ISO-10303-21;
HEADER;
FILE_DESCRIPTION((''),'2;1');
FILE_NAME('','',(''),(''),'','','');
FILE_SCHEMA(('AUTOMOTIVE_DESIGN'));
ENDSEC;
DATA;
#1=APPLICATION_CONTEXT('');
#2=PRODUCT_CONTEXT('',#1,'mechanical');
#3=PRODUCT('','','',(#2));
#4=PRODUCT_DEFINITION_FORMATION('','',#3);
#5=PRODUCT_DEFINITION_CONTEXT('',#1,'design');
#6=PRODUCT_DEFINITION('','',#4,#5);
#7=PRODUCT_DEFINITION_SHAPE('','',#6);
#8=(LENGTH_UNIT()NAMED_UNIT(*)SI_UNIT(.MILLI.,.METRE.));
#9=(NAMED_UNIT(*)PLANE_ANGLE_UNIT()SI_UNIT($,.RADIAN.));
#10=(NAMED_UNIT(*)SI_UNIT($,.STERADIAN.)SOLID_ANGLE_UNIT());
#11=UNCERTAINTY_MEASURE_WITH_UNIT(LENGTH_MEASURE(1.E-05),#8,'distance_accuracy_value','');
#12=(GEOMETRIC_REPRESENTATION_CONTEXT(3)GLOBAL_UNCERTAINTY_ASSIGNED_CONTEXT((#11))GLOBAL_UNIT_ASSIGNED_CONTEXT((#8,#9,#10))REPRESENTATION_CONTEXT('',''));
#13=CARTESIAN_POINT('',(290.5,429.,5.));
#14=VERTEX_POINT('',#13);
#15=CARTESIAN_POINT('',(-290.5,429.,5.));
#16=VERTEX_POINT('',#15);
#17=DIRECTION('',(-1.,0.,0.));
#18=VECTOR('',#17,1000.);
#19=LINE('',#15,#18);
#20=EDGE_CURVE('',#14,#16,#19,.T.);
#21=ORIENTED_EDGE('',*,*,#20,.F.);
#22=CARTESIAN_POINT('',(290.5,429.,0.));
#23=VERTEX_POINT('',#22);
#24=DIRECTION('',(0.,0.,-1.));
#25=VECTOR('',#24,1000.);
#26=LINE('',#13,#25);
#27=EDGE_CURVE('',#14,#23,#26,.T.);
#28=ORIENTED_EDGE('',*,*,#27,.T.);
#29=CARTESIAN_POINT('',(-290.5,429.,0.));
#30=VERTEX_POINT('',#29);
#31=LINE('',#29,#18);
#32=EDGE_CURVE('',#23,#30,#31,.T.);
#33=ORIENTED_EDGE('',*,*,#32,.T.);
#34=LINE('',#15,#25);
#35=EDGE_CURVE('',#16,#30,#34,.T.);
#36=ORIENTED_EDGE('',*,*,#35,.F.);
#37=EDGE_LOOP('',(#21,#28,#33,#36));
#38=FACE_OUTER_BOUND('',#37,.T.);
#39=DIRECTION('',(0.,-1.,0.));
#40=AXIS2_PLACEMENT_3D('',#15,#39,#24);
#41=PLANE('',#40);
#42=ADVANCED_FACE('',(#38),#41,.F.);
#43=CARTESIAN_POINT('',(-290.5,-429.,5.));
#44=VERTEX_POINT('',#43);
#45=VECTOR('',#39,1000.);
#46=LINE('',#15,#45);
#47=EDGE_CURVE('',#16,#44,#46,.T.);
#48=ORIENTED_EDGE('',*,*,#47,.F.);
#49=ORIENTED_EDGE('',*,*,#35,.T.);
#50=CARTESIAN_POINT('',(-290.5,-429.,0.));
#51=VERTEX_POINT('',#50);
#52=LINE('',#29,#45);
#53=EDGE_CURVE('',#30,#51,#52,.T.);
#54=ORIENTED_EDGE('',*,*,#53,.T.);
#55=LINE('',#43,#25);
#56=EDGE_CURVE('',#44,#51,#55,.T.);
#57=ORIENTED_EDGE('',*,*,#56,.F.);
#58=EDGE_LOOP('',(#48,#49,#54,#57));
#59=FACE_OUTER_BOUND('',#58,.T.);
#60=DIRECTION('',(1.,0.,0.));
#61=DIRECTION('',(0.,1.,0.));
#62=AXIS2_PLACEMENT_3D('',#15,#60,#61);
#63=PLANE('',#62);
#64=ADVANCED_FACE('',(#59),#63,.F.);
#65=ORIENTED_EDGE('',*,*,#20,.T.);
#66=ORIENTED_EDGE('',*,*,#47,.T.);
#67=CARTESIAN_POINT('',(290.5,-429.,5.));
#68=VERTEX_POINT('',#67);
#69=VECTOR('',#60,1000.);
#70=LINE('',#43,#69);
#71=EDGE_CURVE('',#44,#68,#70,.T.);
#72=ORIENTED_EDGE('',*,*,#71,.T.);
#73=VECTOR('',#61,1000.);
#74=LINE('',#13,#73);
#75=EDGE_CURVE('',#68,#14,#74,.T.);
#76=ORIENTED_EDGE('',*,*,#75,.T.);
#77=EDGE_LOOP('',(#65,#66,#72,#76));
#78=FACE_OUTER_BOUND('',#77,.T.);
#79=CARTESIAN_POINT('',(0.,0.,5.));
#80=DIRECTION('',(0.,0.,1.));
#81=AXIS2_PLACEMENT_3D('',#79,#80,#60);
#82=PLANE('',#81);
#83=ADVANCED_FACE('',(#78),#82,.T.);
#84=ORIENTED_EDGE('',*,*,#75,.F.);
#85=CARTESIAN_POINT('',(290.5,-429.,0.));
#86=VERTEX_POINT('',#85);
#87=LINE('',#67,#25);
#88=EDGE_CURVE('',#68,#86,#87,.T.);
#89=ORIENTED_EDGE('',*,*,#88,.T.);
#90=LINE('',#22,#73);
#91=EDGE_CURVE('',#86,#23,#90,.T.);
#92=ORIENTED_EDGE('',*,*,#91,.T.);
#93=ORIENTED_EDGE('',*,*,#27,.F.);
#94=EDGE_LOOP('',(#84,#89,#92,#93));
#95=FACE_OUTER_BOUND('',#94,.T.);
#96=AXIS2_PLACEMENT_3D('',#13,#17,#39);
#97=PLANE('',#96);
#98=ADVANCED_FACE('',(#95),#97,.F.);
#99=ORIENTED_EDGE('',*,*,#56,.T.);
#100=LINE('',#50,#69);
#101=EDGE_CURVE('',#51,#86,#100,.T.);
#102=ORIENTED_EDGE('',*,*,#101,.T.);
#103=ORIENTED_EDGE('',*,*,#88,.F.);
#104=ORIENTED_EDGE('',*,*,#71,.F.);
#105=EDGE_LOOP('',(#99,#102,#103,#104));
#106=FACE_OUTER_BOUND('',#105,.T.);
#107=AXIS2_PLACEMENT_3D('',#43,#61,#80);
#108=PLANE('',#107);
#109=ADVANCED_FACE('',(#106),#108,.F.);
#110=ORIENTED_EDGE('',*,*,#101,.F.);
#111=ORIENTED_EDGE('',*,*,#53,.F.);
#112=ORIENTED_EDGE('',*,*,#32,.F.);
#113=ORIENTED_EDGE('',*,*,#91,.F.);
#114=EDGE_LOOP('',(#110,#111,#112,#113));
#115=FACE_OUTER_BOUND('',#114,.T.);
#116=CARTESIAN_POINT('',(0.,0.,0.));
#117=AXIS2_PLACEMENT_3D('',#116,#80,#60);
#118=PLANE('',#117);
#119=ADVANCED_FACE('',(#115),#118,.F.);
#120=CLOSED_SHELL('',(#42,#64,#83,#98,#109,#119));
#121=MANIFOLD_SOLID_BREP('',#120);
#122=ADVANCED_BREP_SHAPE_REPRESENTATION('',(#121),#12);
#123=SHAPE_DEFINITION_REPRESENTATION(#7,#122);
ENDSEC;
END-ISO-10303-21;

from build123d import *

# Parameters (mm, degrees)
SKETCH_1_W      = 581
SKETCH_1_H      = 858
EXTRUDE_1_DEPTH = 5


with BuildPart() as part:
    # 草图1 → 凸台-拉伸1 (new body)
    with BuildSketch(Plane.XY):
        Rectangle(SKETCH_1_W, SKETCH_1_H)
    extrude(amount=EXTRUDE_1_DEPTH)


solid = part.part
